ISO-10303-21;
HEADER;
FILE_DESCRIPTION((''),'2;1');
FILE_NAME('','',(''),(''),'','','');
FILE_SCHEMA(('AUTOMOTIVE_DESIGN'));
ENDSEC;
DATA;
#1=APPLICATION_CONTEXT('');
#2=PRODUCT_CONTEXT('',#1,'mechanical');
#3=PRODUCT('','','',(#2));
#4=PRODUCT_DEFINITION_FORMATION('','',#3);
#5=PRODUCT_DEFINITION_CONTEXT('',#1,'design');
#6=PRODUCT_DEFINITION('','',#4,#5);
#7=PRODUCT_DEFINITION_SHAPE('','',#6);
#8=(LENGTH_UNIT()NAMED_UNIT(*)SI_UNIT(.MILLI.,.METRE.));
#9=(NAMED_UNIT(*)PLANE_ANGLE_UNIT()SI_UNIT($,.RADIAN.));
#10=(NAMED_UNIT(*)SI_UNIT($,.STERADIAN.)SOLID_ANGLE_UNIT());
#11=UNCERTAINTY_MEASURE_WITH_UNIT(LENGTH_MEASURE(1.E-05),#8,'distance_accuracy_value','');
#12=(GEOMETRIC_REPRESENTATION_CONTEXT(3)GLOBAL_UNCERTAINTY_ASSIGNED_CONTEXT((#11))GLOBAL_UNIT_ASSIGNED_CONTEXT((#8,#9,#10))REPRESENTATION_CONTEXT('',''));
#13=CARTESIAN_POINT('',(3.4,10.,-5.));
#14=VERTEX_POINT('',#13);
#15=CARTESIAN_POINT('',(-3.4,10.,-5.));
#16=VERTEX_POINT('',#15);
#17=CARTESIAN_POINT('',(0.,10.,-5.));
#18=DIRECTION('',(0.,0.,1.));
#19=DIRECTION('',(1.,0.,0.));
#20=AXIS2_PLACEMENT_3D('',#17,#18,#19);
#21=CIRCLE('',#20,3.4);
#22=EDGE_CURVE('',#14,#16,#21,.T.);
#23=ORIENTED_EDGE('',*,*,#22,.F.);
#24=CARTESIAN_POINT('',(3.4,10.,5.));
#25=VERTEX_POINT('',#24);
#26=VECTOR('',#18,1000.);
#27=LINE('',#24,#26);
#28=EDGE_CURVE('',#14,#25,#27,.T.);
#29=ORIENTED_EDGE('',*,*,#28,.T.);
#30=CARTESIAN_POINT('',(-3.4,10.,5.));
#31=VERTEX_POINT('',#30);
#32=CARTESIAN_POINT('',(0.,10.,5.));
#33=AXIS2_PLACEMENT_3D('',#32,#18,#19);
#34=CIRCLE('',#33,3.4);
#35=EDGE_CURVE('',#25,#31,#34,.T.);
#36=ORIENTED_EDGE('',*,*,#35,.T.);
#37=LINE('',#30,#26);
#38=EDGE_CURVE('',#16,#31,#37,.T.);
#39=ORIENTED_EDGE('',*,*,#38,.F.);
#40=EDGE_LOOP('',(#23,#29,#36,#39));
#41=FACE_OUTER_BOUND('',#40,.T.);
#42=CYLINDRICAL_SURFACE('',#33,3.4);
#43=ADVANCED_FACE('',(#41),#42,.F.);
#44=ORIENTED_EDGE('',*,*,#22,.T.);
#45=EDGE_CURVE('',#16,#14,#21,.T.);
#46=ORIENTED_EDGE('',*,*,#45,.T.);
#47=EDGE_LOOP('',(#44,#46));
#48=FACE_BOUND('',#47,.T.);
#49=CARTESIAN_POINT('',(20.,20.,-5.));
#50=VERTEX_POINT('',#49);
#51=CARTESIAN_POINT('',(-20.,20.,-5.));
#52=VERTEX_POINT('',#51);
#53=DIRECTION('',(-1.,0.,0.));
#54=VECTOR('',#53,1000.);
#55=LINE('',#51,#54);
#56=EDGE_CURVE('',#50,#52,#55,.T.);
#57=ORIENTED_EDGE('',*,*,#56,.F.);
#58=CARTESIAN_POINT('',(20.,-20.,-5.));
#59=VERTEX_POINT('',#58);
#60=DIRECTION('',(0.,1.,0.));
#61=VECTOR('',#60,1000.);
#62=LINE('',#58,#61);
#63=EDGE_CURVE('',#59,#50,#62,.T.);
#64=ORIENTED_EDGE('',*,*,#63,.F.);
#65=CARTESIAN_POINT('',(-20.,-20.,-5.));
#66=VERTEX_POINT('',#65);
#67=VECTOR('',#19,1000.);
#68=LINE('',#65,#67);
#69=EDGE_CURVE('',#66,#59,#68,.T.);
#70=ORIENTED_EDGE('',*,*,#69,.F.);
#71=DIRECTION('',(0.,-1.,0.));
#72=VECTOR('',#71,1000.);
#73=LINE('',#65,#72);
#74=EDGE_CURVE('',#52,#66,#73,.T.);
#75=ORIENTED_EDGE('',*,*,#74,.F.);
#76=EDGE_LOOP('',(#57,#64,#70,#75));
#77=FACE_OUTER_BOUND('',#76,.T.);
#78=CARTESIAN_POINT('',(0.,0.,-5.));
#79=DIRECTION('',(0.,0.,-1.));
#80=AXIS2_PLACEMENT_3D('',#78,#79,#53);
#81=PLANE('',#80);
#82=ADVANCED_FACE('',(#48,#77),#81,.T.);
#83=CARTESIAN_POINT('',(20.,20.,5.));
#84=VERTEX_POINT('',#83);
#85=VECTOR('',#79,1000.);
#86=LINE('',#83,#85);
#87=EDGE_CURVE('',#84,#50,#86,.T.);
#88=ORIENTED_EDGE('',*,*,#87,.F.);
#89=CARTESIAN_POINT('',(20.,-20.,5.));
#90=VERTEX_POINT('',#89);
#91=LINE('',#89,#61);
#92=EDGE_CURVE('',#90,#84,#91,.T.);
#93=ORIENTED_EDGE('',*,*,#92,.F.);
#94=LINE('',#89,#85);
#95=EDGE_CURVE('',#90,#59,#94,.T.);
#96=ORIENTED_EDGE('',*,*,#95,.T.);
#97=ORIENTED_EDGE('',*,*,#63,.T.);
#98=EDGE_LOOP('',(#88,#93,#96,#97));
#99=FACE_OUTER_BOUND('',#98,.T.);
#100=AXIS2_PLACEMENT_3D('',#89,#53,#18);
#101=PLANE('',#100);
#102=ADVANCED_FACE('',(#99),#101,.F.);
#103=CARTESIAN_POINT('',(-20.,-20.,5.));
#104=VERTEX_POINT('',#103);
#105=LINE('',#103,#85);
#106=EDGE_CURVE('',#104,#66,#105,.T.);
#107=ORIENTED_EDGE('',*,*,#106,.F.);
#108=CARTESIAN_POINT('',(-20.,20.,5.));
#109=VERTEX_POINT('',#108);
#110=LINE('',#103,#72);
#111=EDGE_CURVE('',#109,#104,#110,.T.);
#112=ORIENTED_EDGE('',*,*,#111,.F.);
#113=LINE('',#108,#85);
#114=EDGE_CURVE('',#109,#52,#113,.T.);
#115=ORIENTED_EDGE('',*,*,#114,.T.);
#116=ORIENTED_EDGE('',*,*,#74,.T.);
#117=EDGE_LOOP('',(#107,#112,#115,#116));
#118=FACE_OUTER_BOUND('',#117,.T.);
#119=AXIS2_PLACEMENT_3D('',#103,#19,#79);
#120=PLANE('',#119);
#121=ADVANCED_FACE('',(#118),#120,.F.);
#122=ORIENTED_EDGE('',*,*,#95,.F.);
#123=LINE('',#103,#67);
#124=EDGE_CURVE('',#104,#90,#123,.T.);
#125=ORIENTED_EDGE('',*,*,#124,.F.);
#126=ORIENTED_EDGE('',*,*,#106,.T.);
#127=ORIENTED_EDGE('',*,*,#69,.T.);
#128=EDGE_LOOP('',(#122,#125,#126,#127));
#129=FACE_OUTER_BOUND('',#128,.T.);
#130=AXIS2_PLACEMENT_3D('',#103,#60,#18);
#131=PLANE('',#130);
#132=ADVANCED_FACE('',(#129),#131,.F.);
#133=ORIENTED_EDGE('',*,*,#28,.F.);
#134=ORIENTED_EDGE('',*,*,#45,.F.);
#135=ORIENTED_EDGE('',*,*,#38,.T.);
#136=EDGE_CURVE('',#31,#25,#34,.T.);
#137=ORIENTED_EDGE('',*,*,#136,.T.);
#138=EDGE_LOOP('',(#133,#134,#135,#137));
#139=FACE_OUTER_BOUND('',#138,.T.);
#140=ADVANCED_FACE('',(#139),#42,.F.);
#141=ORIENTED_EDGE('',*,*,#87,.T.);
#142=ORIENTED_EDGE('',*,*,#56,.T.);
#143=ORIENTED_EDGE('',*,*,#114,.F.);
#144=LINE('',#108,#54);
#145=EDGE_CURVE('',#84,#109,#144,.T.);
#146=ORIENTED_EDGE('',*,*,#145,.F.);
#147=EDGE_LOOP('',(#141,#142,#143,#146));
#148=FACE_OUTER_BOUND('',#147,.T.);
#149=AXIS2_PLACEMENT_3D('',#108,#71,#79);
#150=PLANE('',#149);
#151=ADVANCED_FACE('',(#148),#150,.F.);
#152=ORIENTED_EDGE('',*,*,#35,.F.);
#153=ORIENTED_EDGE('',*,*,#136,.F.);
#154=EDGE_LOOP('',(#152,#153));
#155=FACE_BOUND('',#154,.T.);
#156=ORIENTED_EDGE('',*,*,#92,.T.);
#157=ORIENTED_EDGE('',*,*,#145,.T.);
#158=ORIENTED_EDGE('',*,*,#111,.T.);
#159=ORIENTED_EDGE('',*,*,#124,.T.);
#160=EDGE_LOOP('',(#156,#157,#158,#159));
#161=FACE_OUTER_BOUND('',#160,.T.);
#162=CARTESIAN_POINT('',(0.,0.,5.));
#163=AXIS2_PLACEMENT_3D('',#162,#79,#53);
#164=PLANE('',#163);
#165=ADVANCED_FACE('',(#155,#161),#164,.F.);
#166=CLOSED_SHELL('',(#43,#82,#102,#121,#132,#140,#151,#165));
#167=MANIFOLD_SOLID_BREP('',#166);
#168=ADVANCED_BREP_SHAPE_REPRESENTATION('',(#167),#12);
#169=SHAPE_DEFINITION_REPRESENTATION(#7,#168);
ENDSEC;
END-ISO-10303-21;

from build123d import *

# Parameters (mm, degrees)
SKETCH_1_W         = 40
SKETCH_1_H         = 40
EXTRUDE_1_DEPTH    = 5
HOLE_WIZARD_M8_1_D = 6.8


with BuildPart() as part:
    # 草图1 → 凸台-拉伸1 (new, symmetric)
    with BuildSketch(Plane.XY):
        Rectangle(SKETCH_1_W, SKETCH_1_H)
    extrude(amount=EXTRUDE_1_DEPTH, both=True)

    # M8 螺纹孔1 (through all)
    with Locations(Plane.XY.offset(5)):
        with Locations((0, 10)):
            Hole(HOLE_WIZARD_M8_1_D / 2)


solid = part.part
